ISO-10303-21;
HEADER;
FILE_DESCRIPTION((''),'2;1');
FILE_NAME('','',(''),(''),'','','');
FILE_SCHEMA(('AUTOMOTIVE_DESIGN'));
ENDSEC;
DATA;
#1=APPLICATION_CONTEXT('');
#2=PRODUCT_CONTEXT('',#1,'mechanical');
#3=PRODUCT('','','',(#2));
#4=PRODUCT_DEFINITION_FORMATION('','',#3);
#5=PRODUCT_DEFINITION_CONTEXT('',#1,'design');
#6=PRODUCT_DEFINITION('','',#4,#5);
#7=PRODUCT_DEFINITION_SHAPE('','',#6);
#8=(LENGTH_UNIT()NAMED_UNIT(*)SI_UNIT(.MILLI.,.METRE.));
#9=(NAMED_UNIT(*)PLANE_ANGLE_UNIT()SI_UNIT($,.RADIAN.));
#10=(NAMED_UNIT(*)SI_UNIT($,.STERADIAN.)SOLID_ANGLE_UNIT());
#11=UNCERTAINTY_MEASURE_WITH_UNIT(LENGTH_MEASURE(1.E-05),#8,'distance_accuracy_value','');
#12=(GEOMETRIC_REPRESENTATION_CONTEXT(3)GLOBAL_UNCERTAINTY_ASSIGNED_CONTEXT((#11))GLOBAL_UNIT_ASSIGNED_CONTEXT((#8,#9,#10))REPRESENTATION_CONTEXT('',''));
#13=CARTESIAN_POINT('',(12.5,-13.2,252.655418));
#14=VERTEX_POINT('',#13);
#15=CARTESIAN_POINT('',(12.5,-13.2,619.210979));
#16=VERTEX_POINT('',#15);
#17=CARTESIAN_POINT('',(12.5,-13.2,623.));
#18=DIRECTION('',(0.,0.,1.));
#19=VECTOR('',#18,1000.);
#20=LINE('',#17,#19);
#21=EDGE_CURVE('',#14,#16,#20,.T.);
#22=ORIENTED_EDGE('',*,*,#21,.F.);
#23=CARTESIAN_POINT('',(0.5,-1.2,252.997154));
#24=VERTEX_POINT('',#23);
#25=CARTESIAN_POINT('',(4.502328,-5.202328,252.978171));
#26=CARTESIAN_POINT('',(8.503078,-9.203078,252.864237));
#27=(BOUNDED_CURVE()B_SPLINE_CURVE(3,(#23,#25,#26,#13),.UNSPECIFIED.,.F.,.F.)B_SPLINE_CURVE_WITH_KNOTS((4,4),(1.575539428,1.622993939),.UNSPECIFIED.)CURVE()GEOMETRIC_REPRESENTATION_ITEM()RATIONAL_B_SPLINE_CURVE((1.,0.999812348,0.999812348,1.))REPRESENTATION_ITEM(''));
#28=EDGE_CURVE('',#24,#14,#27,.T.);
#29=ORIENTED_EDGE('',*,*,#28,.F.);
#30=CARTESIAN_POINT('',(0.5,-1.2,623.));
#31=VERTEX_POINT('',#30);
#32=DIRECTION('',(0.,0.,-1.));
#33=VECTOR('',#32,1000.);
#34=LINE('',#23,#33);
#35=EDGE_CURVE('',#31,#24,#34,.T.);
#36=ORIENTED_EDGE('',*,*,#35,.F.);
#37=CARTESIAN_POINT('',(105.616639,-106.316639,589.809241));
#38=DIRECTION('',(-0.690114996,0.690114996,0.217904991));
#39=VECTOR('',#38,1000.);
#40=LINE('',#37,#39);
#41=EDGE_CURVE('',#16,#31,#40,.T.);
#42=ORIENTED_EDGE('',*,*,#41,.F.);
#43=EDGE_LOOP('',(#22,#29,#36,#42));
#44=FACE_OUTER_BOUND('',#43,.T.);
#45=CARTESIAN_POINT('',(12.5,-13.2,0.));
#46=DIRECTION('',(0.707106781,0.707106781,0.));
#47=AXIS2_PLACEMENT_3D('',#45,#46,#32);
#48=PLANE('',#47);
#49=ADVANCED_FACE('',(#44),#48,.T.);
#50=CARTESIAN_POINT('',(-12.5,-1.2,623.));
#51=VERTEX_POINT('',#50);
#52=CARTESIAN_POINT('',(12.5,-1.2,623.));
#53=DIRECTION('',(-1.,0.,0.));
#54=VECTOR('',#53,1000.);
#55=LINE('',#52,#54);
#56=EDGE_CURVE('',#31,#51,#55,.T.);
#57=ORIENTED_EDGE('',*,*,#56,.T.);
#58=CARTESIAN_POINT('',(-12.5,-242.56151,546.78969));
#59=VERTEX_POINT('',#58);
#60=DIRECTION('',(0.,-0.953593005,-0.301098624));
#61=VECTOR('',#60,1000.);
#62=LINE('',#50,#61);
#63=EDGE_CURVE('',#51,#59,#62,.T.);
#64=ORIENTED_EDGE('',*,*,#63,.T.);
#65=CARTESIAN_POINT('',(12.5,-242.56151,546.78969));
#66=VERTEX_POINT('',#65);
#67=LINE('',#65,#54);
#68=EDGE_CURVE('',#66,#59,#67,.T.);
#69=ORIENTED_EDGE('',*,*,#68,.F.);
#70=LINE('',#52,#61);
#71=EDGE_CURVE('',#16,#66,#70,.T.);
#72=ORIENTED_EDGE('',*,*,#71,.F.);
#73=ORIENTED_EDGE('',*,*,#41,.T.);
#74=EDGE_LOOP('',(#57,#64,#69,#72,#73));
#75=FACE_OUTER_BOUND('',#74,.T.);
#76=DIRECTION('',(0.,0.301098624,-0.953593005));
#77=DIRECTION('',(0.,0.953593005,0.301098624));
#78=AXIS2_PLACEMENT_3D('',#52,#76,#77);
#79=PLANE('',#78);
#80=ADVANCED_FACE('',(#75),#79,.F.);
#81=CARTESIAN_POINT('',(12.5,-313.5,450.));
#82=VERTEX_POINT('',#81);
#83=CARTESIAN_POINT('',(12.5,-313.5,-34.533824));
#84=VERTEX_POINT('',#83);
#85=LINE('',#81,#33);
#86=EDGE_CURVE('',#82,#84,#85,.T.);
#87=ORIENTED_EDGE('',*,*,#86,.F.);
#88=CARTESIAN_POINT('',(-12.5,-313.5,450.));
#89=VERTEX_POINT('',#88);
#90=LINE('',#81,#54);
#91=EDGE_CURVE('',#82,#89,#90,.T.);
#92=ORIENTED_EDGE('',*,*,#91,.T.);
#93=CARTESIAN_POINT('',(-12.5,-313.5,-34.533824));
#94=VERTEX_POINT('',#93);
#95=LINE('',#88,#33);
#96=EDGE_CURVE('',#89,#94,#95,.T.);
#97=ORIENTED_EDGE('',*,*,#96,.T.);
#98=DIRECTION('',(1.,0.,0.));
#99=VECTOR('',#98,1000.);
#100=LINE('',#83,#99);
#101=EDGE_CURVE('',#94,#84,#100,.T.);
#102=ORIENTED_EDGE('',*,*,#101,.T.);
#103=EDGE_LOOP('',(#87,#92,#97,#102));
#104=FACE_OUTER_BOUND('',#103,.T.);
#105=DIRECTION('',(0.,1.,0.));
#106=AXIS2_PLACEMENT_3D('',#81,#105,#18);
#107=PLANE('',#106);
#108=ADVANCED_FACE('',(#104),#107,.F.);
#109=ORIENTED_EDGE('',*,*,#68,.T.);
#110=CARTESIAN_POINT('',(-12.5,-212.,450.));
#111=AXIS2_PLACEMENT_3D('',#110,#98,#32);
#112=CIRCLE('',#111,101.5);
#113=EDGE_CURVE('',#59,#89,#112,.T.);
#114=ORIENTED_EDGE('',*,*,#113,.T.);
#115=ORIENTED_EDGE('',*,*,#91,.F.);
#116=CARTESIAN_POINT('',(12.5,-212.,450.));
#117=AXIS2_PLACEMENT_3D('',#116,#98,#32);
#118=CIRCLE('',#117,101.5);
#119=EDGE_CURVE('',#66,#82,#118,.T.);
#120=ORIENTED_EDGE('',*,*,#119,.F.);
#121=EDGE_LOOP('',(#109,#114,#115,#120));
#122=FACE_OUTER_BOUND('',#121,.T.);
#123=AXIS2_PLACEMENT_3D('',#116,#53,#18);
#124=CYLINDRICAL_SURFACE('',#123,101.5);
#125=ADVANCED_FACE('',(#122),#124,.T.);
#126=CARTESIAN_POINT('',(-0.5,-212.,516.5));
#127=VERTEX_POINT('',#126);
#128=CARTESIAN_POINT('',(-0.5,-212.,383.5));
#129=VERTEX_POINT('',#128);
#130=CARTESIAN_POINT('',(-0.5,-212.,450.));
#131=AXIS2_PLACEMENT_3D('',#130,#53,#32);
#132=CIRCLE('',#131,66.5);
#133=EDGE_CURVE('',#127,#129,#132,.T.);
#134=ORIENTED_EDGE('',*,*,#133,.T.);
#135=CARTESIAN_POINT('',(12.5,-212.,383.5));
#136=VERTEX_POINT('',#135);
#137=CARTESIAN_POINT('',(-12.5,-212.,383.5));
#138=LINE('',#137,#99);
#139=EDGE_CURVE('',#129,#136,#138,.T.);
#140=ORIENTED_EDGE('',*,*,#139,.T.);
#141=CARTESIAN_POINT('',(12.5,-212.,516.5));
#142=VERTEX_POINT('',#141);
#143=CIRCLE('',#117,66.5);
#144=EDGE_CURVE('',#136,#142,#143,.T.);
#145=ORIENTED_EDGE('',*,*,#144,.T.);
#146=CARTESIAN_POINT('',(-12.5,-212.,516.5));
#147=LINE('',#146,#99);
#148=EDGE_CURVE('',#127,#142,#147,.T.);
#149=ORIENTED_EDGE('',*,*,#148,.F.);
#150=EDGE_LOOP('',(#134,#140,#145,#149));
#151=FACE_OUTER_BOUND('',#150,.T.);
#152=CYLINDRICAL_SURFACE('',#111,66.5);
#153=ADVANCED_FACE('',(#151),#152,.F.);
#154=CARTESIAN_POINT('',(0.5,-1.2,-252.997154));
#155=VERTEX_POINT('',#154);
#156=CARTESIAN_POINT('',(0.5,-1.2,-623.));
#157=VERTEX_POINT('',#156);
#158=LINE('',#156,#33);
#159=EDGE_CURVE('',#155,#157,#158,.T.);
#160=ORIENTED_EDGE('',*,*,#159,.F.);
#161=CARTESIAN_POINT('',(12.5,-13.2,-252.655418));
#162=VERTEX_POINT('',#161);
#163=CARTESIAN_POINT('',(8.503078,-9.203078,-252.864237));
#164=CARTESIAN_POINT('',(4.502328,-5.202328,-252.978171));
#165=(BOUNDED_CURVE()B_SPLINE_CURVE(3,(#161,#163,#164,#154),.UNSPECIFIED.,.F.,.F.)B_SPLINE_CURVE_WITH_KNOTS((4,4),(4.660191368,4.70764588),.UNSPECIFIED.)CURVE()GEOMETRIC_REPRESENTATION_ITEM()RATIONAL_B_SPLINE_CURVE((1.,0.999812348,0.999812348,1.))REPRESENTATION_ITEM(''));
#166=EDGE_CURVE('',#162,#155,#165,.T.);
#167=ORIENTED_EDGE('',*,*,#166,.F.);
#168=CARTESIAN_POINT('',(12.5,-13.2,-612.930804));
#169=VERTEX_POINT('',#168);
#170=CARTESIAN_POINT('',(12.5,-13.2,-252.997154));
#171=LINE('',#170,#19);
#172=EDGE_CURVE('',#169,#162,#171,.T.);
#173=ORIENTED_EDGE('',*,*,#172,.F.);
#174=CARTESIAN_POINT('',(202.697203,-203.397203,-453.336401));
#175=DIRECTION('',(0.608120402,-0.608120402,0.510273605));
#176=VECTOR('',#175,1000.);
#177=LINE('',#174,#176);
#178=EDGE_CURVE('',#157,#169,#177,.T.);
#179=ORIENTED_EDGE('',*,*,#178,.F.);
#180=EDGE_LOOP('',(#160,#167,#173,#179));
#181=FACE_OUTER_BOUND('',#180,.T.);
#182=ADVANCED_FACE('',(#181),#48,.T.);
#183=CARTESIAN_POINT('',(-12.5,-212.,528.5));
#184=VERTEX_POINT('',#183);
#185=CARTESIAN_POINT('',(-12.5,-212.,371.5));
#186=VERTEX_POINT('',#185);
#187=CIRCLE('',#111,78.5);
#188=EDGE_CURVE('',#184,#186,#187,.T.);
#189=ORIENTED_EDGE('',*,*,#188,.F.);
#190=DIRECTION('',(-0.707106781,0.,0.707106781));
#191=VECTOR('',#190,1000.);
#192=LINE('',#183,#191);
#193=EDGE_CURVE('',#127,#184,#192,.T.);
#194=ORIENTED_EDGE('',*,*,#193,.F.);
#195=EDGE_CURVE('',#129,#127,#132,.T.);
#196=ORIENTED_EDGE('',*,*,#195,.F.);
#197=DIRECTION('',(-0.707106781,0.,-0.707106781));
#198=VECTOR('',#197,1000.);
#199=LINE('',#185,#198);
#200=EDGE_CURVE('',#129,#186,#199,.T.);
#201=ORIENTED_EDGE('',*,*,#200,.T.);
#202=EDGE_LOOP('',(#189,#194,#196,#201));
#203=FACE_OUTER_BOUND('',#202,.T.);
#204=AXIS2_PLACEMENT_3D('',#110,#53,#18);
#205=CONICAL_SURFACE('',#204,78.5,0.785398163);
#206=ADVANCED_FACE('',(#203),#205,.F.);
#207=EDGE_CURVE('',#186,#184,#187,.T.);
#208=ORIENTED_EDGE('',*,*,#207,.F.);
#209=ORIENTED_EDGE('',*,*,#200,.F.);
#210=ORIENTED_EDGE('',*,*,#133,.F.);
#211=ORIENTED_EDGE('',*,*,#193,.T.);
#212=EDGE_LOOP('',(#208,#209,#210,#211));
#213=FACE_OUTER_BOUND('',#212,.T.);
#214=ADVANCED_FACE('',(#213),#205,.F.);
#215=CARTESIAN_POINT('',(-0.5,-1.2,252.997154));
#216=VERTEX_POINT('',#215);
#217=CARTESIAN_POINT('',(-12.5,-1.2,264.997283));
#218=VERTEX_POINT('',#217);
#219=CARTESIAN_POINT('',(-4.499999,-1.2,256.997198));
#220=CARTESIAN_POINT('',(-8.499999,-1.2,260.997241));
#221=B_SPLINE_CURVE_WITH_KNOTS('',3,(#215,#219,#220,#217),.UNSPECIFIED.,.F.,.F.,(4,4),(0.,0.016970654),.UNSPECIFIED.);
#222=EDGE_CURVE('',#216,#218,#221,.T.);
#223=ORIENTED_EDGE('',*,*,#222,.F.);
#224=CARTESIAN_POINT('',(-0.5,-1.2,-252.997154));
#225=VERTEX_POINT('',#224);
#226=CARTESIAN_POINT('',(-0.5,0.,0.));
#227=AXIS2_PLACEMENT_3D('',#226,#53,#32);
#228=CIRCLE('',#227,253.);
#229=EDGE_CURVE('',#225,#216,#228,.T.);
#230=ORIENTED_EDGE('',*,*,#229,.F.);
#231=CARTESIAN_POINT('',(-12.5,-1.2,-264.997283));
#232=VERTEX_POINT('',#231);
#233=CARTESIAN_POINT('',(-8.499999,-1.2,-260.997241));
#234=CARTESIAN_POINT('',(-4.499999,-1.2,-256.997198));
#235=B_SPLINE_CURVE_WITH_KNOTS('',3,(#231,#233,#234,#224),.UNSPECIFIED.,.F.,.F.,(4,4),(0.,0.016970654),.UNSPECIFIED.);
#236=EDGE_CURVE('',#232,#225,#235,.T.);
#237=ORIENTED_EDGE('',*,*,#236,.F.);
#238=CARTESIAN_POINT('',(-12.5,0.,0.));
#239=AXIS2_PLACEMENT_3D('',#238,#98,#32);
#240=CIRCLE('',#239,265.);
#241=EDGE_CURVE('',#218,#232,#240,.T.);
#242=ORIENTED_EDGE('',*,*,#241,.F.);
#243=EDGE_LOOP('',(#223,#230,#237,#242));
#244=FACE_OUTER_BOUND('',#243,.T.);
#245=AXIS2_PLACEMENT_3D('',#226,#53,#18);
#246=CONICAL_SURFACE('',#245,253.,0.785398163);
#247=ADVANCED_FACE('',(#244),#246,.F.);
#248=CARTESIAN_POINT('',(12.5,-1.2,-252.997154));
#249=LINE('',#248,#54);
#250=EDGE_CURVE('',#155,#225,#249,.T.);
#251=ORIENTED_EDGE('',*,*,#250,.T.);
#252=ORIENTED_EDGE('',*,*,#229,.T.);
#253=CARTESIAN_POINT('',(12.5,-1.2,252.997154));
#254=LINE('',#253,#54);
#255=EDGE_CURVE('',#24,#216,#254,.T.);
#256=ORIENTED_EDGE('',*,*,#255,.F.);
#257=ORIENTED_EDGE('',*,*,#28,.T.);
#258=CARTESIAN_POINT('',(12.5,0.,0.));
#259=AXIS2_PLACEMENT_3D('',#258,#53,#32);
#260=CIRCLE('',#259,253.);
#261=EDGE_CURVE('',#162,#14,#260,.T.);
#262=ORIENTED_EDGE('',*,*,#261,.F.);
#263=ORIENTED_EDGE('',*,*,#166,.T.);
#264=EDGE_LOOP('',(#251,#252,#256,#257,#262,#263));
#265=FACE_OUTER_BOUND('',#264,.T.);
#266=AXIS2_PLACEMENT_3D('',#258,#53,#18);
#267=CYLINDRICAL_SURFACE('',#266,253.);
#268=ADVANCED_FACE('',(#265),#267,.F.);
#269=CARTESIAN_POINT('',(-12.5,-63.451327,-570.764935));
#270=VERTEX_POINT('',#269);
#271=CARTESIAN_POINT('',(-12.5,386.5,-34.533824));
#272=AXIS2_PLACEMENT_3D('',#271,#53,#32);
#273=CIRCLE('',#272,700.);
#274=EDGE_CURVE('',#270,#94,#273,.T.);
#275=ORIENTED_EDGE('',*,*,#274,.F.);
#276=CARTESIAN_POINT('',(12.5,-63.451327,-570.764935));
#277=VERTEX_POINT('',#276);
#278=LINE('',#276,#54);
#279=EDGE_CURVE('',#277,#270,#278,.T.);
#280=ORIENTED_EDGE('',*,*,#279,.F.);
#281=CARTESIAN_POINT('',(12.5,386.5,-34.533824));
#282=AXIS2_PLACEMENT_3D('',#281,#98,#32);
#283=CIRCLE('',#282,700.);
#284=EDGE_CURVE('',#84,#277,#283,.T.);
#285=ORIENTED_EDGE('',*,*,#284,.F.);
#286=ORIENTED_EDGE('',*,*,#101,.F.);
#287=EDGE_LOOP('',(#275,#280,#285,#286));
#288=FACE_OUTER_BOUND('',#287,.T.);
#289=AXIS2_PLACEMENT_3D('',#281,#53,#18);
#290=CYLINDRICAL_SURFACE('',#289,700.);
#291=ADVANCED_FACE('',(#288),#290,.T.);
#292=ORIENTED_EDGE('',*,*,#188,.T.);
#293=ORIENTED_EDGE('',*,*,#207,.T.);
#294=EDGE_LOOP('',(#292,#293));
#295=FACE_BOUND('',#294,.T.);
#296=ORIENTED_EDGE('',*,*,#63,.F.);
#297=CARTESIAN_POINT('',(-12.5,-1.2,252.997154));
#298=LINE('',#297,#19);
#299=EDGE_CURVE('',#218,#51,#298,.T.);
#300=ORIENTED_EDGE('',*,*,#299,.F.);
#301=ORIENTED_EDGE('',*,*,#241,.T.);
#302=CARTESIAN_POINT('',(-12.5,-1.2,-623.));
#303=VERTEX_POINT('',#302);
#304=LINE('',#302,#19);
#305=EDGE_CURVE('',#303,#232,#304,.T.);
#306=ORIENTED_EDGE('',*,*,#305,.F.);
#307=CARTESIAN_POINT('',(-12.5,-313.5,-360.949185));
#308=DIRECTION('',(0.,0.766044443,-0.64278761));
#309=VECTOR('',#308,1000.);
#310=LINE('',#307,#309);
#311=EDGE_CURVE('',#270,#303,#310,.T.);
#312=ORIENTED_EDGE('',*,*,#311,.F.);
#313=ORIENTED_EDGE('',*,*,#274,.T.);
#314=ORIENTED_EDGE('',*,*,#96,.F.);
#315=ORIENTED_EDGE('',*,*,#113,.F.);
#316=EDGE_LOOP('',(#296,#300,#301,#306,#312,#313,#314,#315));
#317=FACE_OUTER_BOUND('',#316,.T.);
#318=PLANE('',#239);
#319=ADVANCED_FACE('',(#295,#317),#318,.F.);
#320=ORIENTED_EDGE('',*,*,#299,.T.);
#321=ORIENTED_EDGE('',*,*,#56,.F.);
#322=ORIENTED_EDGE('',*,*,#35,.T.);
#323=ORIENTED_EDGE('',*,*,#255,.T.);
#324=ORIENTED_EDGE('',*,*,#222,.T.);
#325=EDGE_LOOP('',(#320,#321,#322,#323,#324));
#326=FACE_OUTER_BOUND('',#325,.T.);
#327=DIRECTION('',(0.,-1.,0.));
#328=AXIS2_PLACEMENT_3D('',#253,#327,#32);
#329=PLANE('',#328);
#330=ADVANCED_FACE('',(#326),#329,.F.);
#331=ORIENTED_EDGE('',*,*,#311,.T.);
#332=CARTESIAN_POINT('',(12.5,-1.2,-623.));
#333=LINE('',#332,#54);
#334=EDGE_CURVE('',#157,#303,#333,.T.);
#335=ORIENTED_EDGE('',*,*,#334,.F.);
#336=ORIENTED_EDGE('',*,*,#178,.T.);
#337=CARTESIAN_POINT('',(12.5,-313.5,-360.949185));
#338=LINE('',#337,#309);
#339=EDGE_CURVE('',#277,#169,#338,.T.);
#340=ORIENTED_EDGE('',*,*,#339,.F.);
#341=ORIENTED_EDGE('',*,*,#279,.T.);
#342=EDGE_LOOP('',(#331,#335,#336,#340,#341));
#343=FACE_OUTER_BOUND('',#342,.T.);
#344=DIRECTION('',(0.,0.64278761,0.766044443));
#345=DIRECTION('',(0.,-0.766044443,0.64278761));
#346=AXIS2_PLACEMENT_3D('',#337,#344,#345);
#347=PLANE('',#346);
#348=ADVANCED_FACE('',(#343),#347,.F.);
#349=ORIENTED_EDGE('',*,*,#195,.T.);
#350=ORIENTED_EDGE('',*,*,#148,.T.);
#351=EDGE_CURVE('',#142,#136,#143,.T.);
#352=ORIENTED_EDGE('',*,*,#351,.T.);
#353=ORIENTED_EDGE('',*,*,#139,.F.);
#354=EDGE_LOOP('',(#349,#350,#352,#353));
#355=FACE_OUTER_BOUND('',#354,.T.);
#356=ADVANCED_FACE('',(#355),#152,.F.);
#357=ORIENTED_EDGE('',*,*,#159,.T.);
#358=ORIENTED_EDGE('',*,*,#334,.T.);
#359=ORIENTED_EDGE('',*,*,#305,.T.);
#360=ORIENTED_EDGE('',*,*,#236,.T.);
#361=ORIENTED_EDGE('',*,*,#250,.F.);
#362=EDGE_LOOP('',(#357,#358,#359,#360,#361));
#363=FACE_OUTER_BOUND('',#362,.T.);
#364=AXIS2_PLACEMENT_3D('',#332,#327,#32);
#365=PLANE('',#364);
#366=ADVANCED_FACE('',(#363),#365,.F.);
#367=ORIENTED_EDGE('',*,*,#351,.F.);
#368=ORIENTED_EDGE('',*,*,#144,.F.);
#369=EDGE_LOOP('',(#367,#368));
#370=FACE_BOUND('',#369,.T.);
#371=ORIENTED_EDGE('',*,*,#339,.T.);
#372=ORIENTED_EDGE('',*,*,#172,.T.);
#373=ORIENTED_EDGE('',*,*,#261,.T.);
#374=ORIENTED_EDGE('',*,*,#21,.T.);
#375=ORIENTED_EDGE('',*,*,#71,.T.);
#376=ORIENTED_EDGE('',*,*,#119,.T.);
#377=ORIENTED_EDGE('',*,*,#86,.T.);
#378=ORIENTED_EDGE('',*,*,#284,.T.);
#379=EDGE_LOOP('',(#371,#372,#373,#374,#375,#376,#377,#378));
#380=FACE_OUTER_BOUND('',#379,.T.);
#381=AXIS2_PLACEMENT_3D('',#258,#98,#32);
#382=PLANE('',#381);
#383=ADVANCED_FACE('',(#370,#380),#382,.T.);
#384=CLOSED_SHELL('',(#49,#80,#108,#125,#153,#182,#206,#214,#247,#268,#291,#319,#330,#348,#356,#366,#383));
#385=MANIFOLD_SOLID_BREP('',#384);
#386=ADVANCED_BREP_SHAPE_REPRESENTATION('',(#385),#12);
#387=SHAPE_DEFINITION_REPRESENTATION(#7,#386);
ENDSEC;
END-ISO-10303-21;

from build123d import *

# Parameters (mm, degrees)
BOSS_EXTRUDE1_DEPTH     = 12.5
CUT_EXTRUDE1_DEPTH      = 698.543905428
CUT_EXTRUDE1_DEPTH_BACK = 698.543905428
SKETCH2_R               = 66.5
FILLET1_R               = 700
CHAMFER1_SIZE           = 12
CHAMFER2_SIZE           = 12


with BuildPart() as part:
    # Sketch1 → Boss-Extrude1 (new, symmetric)
    with BuildSketch(Plane(origin=(0, 0, 0), x_dir=(0, 0, -1), z_dir=(1, 0, 0))):
        with BuildLine():
            Line((623, -1.2), (252.997154134, -1.2))
            ThreePointArc((252.997154134, -1.2), (0, -253), (-252.997154134, -1.2))
            Line((-252.997154134, -1.2), (-623, -1.2))
            Line((-623, -1.2), (-546.789689993, -242.561510288))
            ThreePointArc((-546.789689993, -242.561510288), (-510.001069598, -293.866486715), (-450, -313.5))
            Line((-450, -313.5), (360.949185183, -313.5))
            Line((360.949185183, -313.5), (623, -1.2))
        make_face()
    extrude(amount=BOSS_EXTRUDE1_DEPTH, both=True)

    # Sketch2 → Cut-Extrude1 (cut, two sides: drawn at the far end of the back side and taken through both)
    with BuildSketch(Plane(origin=(0, 0, 0), x_dir=(0, 0, -1), z_dir=(1, 0, 0)).offset(-CUT_EXTRUDE1_DEPTH_BACK)):
        with Locations((-450, -212)):
            Circle(SKETCH2_R)
    extrude(amount=CUT_EXTRUDE1_DEPTH + CUT_EXTRUDE1_DEPTH_BACK, mode=Mode.SUBTRACT)

    # Fillet1
    fillet1_edges = [part.edges().sort_by_distance(p)[0] for p in [
        (0, -313.5, -360.949185183),
    ]]
    fillet(fillet1_edges, radius=FILLET1_R)

    # Chamfer1
    chamfer1_edges = [part.edges().sort_by_distance(p)[0] for p in [
        (-12.5, -212, 516.5),
        (-12.5, -253, 0),
    ]]
    chamfer(chamfer1_edges, length=CHAMFER1_SIZE)

    # Chamfer2
    chamfer2_edges = [part.edges().sort_by_distance(p)[0] for p in [
        (12.5, -1.2, -437.998577067),
        (12.5, -1.2, 437.998577067),
    ]]
    chamfer(chamfer2_edges, length=CHAMFER2_SIZE)


solid = part.part
